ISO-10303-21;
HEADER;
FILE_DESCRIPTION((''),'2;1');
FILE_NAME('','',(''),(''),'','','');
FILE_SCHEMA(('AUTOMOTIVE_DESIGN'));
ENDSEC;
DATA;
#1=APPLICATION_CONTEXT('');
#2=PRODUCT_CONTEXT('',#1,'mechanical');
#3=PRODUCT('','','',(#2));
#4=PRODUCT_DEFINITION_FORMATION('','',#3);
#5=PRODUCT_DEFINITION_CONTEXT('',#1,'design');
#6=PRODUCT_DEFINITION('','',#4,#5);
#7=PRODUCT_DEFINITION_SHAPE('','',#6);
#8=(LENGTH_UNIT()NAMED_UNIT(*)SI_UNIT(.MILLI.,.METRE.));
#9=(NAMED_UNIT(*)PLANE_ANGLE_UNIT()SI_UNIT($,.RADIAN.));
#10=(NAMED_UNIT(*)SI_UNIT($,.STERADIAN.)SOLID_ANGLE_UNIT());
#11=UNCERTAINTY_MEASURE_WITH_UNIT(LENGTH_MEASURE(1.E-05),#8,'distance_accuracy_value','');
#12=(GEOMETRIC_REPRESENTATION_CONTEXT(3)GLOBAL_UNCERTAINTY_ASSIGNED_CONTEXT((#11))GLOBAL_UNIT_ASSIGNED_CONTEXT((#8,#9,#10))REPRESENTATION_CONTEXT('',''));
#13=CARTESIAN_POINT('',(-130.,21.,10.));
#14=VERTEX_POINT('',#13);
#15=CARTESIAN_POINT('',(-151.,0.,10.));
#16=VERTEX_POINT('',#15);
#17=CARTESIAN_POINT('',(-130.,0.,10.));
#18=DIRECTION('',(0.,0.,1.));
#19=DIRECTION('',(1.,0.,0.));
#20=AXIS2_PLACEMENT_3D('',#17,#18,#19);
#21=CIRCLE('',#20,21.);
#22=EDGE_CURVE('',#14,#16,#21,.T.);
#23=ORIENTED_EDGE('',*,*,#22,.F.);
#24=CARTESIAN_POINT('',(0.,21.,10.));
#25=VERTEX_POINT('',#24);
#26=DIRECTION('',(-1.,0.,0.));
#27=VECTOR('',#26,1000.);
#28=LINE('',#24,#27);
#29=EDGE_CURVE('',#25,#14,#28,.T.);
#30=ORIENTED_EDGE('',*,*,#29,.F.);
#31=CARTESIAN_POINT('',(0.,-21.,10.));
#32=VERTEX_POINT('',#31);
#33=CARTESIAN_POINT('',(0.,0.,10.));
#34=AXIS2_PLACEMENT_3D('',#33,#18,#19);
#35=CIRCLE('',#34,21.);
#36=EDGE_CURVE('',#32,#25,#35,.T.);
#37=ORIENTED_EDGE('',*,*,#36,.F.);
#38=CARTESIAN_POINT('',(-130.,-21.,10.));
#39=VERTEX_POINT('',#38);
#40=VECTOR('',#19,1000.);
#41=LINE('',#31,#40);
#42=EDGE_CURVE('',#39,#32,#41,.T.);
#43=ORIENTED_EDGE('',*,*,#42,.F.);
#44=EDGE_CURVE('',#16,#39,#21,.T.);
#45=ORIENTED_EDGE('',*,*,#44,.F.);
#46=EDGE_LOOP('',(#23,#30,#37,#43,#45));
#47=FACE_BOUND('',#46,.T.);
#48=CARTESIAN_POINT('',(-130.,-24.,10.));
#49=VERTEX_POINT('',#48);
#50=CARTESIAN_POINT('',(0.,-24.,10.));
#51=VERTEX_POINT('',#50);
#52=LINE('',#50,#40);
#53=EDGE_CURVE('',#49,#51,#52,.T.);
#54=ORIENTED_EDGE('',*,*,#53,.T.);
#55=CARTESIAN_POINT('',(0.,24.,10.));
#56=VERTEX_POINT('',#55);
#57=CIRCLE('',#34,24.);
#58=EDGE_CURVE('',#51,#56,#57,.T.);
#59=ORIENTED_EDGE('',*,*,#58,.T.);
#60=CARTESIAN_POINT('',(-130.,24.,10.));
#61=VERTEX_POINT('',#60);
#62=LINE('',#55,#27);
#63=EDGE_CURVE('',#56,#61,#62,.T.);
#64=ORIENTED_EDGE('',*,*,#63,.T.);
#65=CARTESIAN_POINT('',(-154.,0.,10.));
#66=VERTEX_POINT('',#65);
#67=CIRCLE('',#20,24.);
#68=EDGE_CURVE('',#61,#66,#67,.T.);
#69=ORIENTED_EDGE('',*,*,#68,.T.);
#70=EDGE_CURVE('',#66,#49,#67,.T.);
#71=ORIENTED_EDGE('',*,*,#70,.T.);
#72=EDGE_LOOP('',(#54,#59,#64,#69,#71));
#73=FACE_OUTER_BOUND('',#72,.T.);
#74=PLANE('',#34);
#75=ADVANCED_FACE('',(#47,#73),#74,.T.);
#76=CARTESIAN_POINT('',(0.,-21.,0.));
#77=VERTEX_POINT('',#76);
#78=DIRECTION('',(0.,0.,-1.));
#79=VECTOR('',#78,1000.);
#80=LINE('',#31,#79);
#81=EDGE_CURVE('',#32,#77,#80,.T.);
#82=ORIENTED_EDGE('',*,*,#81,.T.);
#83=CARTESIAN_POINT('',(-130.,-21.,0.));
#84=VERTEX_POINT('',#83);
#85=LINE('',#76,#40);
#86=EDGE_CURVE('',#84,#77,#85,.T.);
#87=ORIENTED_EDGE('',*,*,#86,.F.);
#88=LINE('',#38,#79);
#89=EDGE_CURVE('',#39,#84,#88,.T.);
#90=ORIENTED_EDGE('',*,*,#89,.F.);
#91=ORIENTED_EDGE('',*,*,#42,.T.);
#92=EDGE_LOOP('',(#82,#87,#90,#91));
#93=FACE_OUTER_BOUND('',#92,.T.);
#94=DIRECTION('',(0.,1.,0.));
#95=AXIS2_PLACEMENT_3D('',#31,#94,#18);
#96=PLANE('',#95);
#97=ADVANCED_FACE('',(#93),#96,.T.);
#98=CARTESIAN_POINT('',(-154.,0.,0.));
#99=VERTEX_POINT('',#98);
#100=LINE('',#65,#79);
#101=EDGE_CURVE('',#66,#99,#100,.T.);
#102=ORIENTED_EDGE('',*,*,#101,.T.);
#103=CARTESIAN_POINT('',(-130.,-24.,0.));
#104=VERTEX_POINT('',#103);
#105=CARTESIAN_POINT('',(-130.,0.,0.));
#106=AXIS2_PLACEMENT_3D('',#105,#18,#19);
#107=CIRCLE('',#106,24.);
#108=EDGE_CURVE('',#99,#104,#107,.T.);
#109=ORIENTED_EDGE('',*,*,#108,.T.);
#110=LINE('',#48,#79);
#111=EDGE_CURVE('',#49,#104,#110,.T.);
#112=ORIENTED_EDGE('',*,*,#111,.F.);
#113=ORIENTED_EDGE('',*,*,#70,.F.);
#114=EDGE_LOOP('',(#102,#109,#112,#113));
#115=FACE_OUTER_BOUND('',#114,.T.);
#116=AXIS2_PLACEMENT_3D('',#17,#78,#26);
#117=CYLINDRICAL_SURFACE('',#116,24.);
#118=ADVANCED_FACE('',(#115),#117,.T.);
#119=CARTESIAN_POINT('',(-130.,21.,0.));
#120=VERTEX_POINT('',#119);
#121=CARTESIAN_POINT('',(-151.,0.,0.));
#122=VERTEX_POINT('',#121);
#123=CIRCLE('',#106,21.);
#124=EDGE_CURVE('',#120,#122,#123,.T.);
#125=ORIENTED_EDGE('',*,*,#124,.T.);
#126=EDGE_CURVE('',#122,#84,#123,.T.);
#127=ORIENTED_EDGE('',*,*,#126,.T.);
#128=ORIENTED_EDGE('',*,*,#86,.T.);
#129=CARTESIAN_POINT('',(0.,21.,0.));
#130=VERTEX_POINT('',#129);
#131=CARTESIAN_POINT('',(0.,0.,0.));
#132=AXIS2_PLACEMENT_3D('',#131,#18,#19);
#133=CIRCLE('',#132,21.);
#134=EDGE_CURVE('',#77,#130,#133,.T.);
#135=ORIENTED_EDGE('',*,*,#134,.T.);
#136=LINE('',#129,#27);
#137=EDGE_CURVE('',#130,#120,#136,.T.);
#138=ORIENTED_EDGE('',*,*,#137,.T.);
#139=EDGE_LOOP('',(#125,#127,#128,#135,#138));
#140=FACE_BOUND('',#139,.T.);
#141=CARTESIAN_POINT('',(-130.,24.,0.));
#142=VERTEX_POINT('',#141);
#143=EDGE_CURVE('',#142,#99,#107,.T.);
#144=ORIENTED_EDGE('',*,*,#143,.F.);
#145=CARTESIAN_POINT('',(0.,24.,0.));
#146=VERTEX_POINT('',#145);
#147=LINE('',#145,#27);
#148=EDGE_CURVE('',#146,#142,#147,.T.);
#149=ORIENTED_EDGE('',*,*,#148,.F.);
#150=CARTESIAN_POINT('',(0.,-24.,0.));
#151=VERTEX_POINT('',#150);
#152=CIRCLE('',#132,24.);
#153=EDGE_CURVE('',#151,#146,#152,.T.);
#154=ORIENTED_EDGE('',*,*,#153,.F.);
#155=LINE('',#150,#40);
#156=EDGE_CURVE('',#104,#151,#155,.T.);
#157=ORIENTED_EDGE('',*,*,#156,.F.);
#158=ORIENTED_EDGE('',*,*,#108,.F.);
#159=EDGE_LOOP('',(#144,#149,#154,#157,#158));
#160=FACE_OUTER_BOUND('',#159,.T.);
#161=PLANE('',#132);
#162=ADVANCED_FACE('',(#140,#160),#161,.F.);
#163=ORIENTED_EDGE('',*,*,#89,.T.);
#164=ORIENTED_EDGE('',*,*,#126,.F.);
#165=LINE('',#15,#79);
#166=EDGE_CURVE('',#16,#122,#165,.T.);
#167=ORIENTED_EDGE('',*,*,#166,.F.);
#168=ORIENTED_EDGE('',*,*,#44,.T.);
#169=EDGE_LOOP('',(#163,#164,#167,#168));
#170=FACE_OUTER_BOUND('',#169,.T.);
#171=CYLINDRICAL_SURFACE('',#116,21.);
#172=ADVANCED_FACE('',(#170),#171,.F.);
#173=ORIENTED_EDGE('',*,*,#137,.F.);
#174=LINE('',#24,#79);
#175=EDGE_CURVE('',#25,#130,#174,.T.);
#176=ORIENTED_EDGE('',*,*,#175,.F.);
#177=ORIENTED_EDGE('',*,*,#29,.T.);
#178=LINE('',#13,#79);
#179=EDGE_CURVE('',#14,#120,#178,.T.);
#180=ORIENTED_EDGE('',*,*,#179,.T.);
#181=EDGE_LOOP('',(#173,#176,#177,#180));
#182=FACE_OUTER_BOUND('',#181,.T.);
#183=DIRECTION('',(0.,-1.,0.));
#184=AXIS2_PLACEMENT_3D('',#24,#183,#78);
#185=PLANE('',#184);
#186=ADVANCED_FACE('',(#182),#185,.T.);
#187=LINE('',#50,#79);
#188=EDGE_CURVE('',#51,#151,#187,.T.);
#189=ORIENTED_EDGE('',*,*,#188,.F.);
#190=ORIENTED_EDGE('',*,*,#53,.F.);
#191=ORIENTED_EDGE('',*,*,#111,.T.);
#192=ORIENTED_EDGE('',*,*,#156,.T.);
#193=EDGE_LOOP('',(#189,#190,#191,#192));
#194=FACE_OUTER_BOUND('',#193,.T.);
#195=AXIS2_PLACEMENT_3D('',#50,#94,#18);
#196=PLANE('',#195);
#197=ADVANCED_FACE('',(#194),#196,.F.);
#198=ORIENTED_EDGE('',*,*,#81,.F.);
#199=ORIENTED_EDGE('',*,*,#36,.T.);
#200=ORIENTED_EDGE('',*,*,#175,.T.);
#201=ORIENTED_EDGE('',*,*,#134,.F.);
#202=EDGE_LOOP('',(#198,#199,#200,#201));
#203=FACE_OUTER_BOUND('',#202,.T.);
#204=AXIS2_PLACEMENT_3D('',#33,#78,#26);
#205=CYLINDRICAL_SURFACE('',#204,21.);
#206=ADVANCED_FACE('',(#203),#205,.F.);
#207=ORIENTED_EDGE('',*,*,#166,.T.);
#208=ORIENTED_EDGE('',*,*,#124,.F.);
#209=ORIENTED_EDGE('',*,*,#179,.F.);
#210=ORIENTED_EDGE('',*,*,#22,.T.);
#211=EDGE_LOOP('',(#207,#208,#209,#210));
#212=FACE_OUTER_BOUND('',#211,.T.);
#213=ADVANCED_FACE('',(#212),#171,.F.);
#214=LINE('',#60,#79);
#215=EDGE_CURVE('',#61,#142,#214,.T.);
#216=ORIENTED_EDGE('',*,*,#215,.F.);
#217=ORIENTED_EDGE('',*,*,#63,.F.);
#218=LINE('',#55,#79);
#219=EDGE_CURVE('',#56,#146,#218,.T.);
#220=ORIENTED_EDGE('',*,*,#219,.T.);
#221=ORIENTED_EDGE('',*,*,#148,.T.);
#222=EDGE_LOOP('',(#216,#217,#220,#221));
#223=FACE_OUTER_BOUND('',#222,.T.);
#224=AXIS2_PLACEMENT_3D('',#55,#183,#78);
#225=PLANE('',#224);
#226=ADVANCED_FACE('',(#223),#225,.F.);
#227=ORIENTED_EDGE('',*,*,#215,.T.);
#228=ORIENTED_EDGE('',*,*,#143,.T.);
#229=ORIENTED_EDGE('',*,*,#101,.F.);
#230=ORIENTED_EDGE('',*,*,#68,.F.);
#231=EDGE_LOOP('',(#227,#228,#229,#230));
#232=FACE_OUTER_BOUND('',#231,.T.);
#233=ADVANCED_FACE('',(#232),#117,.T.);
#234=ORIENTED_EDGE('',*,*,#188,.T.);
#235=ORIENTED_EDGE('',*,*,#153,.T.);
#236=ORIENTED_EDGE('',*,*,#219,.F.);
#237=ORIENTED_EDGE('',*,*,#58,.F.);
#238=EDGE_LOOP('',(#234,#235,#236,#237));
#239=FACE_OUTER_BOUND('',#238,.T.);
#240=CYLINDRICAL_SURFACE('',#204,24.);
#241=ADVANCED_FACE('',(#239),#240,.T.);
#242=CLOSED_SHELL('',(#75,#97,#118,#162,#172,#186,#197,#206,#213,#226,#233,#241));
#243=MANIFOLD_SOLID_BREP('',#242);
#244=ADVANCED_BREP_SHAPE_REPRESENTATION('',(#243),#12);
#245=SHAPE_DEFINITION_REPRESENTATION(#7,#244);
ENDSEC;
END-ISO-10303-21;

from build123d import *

# Parameters (mm, degrees)
BOSS_EXTRUDE1_DEPTH = 10
SHELL1_T            = -3


with BuildPart() as part:
    # Sketch2 → Boss-Extrude1 (new body)
    with BuildSketch(Plane.XY):
        with BuildLine():
            Line((0, 24), (-130, 24))
            ThreePointArc((-130, 24), (-154, 0), (-130, -24))
            Line((-130, -24), (0, -24))
            ThreePointArc((0, -24), (24, 0), (0, 24))
        make_face()
    extrude(amount=BOSS_EXTRUDE1_DEPTH)

    # Shell1
    shell1_openings = [part.faces().sort_by_distance(p)[0] for p in [
        (-65, 0, 10),
        (-65, 0, 0),
    ]]
    offset(amount=SHELL1_T, openings=shell1_openings, kind=Kind.INTERSECTION)


solid = part.part
